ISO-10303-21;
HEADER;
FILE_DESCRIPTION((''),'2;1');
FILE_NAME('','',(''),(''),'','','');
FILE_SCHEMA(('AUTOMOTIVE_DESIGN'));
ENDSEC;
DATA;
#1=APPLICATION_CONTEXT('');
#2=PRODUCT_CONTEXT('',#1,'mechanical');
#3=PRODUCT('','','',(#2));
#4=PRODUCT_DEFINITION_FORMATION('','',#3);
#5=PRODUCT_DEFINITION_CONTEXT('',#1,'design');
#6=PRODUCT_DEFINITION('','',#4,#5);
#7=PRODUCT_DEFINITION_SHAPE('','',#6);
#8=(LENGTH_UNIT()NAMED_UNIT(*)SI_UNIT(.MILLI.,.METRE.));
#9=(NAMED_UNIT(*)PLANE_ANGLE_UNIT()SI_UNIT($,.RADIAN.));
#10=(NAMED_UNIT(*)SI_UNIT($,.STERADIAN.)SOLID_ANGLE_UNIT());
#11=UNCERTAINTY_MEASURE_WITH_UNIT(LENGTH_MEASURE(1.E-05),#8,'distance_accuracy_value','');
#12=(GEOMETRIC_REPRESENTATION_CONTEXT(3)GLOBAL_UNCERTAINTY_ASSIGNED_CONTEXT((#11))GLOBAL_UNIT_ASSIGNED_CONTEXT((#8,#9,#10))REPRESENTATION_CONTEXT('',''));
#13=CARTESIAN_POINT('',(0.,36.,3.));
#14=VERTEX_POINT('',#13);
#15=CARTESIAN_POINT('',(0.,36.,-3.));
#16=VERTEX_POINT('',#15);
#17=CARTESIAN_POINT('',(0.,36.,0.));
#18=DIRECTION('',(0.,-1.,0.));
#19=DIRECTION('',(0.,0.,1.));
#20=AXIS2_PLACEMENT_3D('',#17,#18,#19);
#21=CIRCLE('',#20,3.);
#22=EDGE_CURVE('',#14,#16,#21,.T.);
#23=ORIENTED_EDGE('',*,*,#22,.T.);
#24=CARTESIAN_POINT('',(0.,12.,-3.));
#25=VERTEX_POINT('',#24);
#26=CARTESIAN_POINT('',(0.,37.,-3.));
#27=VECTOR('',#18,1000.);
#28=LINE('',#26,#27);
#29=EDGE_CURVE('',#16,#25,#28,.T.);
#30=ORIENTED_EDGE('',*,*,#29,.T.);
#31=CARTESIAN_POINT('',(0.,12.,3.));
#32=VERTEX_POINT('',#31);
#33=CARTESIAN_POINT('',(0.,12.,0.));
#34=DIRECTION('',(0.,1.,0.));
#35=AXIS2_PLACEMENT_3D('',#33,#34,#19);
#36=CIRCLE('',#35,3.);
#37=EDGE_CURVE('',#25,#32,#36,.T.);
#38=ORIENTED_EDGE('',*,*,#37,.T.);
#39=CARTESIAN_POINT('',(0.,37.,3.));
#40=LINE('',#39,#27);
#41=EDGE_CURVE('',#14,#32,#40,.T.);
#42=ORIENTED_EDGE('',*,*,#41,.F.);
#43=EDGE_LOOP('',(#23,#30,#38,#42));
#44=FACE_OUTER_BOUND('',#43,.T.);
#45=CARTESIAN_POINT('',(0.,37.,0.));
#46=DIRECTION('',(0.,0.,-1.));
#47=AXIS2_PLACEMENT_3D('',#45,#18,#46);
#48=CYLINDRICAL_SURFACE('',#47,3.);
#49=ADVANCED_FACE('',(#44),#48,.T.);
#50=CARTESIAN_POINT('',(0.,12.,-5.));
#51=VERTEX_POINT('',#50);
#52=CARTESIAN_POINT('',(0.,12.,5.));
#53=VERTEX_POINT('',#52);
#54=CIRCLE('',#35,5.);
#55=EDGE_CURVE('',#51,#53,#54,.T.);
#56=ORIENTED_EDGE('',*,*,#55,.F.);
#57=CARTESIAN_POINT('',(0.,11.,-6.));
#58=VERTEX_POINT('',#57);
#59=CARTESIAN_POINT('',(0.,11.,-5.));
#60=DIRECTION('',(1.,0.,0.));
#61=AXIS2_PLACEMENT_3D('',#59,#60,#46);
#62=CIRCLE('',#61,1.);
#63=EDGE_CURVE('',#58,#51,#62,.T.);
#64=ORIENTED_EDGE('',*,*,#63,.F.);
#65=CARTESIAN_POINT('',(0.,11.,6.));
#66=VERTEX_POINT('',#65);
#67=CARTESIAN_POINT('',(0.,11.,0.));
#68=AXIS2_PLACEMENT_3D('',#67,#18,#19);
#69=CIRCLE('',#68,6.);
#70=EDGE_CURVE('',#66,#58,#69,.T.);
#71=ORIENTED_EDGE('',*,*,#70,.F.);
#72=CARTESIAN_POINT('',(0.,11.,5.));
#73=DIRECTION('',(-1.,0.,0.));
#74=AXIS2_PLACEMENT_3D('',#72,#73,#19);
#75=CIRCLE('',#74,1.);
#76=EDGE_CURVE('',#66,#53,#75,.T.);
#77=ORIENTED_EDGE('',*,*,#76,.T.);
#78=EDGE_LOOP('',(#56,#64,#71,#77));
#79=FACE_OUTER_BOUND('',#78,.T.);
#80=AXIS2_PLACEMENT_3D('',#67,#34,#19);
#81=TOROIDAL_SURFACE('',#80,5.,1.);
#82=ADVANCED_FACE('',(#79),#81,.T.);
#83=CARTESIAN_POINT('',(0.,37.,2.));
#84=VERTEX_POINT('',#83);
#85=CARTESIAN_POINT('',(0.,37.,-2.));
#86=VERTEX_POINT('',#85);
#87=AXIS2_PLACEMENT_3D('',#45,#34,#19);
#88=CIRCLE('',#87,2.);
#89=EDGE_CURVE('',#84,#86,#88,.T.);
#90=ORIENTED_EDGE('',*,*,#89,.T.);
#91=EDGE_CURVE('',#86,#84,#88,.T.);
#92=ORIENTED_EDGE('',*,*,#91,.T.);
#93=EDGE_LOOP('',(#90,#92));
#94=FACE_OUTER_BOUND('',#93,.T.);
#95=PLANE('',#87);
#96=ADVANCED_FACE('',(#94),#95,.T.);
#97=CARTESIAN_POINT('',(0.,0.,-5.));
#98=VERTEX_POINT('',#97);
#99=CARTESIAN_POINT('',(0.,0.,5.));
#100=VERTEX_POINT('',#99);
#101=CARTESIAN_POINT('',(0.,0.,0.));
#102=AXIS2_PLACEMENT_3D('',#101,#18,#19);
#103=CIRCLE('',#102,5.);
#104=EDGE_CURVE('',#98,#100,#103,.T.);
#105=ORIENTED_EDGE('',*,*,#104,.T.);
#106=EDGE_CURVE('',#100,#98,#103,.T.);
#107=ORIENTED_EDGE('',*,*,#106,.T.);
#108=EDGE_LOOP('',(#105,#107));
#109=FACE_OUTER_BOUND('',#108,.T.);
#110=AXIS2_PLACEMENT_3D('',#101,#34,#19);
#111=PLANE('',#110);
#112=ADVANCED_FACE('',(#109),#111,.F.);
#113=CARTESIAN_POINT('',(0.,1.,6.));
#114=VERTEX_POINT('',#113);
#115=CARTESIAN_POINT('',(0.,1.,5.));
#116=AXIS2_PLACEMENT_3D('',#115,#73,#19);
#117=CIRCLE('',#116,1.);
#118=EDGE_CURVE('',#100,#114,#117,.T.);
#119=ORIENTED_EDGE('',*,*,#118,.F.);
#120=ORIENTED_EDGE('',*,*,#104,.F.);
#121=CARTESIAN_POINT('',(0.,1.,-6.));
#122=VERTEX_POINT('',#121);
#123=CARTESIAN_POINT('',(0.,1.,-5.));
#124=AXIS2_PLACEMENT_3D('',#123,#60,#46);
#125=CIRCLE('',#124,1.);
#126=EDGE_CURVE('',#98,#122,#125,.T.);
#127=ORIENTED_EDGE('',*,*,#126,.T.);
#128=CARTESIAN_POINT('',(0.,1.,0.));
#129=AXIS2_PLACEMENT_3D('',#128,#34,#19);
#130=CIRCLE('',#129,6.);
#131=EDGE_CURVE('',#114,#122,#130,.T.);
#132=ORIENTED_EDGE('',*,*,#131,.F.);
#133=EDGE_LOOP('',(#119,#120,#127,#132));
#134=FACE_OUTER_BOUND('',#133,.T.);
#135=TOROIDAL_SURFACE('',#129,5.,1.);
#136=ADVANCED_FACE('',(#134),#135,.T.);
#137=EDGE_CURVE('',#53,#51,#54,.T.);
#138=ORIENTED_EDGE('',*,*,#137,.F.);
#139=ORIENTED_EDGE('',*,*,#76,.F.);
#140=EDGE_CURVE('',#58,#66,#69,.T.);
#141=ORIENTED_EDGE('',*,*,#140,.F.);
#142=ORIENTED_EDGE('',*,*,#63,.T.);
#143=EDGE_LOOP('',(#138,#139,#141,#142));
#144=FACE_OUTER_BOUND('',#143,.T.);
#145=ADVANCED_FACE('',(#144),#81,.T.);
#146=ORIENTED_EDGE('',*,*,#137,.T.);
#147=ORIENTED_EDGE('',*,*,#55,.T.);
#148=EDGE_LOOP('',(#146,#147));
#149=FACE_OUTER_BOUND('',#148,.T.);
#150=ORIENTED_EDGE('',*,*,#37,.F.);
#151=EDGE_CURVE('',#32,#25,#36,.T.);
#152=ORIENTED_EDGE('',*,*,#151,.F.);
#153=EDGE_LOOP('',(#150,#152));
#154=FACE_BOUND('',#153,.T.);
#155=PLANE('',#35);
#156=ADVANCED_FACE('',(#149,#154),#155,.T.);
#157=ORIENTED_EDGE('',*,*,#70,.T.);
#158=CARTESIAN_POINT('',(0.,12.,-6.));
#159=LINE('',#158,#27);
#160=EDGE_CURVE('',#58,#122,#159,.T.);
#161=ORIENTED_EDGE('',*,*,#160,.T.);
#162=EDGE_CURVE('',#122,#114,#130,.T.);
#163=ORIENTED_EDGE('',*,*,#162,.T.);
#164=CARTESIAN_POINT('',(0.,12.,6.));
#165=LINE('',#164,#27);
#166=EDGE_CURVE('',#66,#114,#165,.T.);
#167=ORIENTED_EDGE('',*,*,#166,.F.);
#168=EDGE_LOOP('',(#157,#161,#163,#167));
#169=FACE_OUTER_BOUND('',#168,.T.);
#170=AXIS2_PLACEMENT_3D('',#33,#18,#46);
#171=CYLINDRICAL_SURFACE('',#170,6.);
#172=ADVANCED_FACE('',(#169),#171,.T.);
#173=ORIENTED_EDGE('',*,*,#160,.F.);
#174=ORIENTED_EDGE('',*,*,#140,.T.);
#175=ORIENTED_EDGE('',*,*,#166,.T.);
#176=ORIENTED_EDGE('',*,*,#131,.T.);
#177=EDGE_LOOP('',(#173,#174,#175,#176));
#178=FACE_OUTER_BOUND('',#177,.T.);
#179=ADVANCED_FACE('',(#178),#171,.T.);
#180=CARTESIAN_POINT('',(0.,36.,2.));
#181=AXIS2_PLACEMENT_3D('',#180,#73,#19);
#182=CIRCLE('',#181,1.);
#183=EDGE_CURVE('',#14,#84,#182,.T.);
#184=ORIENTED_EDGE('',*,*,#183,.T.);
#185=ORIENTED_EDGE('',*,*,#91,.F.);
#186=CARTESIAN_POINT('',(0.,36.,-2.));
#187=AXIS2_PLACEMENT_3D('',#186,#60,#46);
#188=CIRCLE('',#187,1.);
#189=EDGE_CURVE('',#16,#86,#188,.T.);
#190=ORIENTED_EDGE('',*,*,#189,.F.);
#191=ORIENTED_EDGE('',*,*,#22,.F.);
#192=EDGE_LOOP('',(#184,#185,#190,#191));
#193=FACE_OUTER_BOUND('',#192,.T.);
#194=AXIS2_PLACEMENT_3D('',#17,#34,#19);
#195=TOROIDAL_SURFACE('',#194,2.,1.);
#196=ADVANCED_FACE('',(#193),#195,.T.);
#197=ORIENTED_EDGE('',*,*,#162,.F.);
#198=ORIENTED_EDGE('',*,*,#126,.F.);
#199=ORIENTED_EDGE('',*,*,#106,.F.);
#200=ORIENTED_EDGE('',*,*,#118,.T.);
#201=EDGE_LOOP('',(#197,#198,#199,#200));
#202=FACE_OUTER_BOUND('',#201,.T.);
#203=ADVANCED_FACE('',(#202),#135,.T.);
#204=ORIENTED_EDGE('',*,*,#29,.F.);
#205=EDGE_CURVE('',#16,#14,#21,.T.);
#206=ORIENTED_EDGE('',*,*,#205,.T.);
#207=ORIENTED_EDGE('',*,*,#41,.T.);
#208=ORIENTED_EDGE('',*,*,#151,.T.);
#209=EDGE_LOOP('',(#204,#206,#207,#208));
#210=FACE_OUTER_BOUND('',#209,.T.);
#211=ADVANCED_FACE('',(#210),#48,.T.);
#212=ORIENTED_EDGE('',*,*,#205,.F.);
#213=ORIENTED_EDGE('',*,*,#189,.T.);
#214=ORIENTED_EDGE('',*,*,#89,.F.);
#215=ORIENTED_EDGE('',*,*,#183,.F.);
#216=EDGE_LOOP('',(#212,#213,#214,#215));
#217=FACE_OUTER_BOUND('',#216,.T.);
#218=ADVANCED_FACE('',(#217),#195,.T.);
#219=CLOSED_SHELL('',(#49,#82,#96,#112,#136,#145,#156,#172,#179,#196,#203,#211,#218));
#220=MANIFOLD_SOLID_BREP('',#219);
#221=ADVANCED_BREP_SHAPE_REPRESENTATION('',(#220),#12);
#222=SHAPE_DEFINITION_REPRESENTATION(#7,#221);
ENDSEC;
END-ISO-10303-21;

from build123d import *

# Parameters (mm, degrees)
SKETCH_1_R      = 6
EXTRUDE_1_DEPTH = 12
SKETCH_2_R      = 3
EXTRUDE_2_DEPTH = 25
FILLET_1_R      = 1


with BuildPart() as part:
    # 草图1 → 凸台-拉伸1 (new body)
    with BuildSketch(Plane(origin=(0, 0, 0), x_dir=(1, 0, 0), z_dir=(0, 1, 0))):
        with Locations(Location((0, 0, 0), (0, 0, 270))):
            Circle(SKETCH_1_R)
    extrude(amount=EXTRUDE_1_DEPTH)

    # 草图2 → 凸台-拉伸2 (add)
    with BuildSketch(Plane(origin=(0, 12, 0), x_dir=(1, 0, 0), z_dir=(0, 1, 0))):
        with Locations(Location((0, 0, 0), (0, 0, 270))):
            Circle(SKETCH_2_R)
    extrude(amount=EXTRUDE_2_DEPTH)

    # 圆角1
    fillet_1_edges = [part.edges().sort_by_distance(p)[0] for p in [
        (0, 0, -6),
        (0, 12, -6),
        (0, 37, -3),
    ]]
    fillet(fillet_1_edges, radius=FILLET_1_R)


solid = part.part
